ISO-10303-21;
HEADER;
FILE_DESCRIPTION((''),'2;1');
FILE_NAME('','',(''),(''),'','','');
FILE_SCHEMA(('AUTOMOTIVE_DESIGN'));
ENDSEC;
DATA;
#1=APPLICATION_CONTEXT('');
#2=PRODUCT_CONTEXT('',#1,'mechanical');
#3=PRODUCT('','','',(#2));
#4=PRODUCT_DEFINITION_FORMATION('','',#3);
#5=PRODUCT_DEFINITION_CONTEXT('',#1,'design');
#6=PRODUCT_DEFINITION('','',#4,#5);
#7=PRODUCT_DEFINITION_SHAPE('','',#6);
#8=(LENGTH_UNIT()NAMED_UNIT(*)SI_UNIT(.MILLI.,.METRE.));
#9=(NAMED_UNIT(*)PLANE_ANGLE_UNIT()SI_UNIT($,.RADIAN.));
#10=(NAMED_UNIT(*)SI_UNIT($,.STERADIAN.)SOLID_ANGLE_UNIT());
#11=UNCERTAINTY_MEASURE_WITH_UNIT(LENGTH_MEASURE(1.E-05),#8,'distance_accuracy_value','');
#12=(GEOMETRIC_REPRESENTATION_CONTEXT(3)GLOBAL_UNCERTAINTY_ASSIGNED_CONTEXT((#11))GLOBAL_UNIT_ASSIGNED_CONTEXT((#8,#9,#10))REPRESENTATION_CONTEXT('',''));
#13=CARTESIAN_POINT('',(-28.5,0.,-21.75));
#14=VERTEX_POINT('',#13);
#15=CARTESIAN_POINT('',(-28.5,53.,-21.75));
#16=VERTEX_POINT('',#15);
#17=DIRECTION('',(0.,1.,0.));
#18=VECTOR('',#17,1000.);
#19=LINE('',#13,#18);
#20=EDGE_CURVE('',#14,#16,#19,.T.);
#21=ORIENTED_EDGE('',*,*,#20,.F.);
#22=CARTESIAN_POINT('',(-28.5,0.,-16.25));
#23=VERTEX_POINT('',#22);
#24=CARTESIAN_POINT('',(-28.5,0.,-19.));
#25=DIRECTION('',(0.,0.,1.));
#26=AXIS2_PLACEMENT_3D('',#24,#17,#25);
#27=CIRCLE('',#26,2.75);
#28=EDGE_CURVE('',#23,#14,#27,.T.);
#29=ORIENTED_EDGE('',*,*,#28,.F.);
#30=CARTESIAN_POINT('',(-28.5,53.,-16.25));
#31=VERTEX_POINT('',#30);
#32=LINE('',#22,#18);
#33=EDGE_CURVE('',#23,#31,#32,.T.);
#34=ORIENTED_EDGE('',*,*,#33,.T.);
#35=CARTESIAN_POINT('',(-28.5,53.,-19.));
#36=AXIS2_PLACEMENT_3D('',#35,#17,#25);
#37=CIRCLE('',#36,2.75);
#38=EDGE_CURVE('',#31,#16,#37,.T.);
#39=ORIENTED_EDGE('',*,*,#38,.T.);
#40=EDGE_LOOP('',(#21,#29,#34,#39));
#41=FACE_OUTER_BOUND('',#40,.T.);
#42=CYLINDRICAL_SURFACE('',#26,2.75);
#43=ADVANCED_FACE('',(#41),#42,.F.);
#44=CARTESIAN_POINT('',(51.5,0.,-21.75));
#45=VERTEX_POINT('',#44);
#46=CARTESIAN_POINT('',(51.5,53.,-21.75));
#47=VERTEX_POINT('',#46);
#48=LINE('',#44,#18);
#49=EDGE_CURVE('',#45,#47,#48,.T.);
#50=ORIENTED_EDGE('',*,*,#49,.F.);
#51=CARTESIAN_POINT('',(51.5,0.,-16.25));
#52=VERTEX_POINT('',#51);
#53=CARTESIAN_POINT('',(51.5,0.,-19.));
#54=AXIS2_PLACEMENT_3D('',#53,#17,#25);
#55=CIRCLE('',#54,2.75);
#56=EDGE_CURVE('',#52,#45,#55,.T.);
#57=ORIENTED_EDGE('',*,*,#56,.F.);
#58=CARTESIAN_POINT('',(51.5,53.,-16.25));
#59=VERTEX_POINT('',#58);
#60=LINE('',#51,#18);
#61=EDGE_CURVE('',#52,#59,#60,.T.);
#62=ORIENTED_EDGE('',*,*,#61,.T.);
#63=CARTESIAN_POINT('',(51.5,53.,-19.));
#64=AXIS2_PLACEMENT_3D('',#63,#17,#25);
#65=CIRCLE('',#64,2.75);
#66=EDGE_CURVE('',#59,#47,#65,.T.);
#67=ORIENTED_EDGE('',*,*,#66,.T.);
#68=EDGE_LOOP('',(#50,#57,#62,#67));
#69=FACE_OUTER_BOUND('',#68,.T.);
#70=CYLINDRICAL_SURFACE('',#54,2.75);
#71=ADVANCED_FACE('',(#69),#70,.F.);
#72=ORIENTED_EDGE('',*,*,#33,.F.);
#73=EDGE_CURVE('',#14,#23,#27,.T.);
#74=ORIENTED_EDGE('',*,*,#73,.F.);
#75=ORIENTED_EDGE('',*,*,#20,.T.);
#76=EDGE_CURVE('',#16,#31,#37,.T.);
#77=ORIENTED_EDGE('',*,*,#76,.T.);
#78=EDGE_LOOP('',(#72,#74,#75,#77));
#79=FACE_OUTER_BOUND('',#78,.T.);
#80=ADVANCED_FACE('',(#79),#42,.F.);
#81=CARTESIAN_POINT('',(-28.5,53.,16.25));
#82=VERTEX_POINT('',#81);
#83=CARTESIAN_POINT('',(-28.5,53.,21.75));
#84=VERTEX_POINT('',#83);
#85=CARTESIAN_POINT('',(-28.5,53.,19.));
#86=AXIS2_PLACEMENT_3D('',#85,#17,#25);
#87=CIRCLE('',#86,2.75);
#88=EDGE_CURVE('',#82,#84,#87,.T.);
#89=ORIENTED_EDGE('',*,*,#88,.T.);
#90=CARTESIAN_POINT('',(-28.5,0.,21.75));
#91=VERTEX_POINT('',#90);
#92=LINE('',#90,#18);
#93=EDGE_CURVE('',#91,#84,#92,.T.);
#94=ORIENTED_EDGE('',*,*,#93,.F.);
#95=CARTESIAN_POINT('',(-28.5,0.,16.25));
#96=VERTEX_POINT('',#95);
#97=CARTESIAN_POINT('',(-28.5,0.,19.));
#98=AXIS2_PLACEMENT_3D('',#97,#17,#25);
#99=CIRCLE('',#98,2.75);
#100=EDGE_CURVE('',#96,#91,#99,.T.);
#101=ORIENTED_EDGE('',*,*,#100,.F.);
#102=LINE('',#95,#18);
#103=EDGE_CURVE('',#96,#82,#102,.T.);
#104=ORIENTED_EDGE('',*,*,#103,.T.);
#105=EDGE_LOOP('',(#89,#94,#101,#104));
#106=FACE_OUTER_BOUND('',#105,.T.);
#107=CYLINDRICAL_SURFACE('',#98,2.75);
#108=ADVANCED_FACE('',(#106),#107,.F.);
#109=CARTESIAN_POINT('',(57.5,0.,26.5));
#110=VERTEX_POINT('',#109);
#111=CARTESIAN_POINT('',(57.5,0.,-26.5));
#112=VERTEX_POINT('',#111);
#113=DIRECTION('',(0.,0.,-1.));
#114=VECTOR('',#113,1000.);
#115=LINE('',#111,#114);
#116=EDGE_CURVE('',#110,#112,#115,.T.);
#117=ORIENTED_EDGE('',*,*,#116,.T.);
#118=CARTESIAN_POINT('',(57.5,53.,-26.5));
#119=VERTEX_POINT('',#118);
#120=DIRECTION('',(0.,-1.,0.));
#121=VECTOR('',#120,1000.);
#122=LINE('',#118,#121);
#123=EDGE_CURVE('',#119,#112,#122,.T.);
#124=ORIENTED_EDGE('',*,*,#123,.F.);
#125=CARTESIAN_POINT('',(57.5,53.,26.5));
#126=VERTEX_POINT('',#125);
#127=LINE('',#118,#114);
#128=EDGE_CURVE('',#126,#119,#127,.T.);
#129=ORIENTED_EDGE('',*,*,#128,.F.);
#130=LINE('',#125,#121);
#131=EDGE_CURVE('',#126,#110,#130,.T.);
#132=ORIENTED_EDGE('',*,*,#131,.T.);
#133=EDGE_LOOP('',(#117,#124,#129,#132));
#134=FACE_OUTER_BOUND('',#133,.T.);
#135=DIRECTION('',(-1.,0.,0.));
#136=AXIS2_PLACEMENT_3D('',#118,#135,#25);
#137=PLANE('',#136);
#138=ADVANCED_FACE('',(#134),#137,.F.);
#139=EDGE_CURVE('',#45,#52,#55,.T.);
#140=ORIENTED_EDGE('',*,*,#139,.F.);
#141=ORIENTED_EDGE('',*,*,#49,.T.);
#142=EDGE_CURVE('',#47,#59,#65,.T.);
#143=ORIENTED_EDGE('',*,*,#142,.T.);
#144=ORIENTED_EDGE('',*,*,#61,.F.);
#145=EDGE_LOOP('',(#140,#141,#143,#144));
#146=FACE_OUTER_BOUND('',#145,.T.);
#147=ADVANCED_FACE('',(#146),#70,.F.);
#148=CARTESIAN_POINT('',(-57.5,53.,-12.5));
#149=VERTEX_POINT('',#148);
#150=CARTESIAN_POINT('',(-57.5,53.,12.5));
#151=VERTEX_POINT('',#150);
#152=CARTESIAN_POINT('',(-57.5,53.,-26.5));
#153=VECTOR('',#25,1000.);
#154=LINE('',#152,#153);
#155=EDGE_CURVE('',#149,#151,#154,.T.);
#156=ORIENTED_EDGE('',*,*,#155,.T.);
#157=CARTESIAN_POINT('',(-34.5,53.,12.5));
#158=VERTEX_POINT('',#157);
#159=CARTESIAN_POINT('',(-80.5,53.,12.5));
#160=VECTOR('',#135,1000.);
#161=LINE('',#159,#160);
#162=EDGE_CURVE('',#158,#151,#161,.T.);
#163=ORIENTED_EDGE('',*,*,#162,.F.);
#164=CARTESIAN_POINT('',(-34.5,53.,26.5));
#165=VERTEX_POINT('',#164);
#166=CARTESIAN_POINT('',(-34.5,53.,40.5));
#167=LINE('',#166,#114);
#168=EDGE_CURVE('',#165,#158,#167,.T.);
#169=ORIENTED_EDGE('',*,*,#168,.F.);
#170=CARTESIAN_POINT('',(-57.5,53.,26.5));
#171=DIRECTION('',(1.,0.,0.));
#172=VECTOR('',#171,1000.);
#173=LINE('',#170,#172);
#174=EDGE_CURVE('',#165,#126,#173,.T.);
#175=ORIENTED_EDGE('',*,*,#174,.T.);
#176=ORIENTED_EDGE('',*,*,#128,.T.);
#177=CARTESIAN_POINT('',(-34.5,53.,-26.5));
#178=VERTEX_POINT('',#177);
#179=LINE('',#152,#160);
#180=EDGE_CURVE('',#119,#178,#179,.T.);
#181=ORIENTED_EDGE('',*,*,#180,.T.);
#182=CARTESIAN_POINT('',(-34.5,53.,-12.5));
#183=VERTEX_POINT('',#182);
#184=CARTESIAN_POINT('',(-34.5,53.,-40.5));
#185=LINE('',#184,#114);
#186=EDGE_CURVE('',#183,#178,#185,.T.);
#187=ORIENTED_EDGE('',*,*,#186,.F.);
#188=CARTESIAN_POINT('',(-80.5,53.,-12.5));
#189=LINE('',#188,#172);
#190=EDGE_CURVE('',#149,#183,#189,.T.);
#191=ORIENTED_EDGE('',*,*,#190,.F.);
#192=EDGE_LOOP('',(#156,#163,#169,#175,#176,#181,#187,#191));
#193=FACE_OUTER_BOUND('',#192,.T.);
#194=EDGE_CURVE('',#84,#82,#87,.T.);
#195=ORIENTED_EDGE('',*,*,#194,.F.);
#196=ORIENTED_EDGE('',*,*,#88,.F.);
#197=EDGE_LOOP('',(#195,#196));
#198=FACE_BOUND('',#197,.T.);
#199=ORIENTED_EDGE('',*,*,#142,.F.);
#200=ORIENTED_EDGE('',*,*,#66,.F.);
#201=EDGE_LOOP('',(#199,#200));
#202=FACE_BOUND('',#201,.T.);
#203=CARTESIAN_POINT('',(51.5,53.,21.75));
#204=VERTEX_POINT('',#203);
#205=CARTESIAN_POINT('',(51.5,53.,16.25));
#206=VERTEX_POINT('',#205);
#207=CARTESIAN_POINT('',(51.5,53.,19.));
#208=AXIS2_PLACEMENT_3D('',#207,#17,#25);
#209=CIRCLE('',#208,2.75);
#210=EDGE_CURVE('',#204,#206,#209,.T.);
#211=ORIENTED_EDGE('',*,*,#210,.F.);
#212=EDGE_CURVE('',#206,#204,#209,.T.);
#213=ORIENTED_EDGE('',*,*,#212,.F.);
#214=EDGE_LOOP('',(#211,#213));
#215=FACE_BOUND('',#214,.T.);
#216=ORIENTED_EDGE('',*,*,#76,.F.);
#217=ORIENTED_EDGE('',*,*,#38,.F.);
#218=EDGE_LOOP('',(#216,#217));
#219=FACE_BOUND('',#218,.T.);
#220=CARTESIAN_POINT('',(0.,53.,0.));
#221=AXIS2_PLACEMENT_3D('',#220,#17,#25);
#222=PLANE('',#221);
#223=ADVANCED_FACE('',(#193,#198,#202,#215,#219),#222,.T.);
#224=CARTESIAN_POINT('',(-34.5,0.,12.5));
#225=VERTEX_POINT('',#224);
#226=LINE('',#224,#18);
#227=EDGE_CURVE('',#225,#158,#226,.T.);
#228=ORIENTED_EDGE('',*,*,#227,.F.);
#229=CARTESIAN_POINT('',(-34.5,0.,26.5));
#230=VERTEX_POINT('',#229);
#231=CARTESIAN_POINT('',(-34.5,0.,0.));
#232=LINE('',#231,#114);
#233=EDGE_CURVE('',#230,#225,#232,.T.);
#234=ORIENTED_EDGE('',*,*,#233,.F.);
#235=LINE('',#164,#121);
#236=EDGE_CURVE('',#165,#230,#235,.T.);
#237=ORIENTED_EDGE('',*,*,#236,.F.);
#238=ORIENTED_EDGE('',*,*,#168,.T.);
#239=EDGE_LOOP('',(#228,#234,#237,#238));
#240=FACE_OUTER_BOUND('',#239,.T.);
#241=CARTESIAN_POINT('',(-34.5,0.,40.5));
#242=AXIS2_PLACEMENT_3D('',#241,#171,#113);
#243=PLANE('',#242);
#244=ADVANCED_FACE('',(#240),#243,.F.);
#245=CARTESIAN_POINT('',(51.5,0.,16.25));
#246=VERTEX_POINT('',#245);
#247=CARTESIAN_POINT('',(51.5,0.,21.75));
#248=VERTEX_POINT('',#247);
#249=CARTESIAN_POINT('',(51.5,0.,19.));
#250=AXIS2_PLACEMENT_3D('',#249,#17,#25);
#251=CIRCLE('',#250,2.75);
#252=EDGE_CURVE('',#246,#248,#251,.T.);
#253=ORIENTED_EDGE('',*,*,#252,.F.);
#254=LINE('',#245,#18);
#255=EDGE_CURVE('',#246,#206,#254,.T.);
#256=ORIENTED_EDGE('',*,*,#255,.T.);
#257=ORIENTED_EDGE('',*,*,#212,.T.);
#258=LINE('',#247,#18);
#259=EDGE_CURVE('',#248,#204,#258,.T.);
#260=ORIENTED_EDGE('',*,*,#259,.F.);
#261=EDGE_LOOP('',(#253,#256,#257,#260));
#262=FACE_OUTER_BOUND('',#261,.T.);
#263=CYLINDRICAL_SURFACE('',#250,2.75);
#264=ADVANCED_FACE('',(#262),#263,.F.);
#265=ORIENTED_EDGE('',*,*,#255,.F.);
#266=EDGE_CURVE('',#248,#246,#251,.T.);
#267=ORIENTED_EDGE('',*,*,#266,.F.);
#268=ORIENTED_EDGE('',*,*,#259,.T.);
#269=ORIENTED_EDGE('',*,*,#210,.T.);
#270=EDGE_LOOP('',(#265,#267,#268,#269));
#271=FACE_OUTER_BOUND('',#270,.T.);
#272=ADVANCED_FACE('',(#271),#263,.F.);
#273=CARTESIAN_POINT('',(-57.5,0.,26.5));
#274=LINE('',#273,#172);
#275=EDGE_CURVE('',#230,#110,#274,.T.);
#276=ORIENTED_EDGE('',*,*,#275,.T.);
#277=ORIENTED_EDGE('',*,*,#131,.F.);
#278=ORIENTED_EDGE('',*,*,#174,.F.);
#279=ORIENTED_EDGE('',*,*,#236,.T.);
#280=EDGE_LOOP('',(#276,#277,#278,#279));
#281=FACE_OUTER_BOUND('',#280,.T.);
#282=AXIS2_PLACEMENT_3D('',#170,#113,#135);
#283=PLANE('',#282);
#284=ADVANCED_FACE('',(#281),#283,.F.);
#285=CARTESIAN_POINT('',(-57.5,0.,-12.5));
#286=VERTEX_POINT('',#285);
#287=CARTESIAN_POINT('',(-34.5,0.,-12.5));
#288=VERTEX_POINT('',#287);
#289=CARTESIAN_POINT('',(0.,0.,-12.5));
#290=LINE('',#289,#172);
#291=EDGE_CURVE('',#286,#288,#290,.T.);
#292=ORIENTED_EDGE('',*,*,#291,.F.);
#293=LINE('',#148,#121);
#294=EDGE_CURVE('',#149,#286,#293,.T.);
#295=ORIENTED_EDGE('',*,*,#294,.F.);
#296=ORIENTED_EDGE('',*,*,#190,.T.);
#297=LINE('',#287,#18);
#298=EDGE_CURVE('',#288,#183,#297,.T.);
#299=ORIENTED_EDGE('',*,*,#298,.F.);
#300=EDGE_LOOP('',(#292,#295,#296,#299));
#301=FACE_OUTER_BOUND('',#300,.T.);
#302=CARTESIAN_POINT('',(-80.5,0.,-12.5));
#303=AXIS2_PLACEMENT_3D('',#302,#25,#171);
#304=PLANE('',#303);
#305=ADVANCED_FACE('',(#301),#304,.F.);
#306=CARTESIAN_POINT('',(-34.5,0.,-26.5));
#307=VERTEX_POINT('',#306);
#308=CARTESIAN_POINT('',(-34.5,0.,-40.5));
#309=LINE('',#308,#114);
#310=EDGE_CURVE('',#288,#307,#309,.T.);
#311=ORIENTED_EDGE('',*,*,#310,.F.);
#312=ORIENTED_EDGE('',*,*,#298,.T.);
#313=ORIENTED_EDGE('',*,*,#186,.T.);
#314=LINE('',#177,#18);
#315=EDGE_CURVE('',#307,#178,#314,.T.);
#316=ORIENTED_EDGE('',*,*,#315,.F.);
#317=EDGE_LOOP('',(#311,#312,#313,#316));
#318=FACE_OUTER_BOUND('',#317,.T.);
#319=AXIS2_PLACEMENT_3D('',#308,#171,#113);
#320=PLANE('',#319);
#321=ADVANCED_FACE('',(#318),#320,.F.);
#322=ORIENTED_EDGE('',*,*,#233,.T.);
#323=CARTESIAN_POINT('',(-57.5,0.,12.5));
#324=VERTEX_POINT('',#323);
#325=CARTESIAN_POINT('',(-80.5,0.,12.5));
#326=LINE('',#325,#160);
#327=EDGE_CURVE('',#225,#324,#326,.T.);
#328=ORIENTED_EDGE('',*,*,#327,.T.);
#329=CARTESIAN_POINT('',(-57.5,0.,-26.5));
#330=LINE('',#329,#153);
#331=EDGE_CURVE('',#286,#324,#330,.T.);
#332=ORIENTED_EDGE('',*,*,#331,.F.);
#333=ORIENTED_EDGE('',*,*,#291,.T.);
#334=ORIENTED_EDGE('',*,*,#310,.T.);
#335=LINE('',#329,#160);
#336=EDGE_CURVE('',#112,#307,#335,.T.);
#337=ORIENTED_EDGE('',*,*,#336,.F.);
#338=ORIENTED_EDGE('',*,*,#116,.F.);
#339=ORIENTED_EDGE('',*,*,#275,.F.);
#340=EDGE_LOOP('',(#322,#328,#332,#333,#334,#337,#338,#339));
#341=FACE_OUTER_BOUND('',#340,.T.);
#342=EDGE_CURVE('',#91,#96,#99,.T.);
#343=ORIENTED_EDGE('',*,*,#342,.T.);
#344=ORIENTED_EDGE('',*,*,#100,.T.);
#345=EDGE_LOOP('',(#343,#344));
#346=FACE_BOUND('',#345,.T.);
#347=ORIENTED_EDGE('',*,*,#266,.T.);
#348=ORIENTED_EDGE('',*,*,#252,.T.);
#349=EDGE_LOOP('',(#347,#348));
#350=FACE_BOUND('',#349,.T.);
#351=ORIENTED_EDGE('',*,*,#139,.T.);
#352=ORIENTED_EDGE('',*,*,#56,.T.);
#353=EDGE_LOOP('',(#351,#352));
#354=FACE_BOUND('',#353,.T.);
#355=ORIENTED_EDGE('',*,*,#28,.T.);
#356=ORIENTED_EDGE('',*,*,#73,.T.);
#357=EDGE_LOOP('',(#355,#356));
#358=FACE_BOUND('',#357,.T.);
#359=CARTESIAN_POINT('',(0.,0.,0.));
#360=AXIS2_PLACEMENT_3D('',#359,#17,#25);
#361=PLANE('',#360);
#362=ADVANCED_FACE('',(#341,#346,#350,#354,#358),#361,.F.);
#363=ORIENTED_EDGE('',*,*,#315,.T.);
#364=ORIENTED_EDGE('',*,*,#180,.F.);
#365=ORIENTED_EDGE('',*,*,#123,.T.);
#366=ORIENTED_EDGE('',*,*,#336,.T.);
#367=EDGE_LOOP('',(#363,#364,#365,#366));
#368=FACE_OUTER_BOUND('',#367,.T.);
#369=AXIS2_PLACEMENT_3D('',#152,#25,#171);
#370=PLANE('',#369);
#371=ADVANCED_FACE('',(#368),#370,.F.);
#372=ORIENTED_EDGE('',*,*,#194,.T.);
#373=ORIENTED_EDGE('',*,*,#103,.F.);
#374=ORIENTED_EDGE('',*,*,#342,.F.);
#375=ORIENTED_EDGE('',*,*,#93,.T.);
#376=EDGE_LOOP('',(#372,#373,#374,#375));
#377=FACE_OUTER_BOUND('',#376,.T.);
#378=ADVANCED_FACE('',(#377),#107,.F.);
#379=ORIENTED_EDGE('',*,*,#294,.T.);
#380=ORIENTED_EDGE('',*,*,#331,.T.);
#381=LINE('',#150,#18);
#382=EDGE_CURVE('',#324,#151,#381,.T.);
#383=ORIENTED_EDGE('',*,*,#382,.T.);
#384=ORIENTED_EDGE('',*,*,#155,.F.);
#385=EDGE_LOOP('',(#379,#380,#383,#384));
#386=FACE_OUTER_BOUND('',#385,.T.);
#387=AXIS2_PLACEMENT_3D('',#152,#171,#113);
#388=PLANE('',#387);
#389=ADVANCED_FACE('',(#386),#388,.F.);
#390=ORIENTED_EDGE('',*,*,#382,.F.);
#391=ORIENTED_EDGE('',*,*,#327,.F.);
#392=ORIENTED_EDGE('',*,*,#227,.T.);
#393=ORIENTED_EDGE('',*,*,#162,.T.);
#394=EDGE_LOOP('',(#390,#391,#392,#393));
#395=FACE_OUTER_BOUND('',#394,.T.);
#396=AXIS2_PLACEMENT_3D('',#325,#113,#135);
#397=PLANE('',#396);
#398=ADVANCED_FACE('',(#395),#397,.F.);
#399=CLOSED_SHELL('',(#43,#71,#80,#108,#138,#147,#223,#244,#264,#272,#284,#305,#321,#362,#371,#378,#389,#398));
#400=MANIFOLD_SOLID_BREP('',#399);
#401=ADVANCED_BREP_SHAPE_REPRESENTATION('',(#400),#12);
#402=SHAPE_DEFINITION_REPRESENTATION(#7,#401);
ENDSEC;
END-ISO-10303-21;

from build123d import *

# Parameters (mm, degrees)
SKETCH_1_W          = 115
SKETCH_1_H          = 53
EXTRUDE_1_DEPTH     = 53
SKETCH_2_W          = 46
SKETCH_2_H          = 28
CUT_EXTRUDE_1_DEPTH = 83.568153667
SKETCH_3_R          = 2.75
CUT_EXTRUDE_2_DEPTH = 83.568153667


with BuildPart() as part:
    # 草图1 → 凸台-拉伸1 (new body)
    with BuildSketch(Plane(origin=(0, 0, 0), x_dir=(1, 0, 0), z_dir=(0, 1, 0))):
        Rectangle(SKETCH_1_W, SKETCH_1_H)
    extrude(amount=EXTRUDE_1_DEPTH)

    # 草图2 → 切除-拉伸1 (cut, through all)
    with BuildSketch(Plane(origin=(0, 53, 0), x_dir=(1, 0, 0), z_dir=(0, 1, 0))):
        with Locations((-57.5, -26.5)):
            Rectangle(SKETCH_2_W, SKETCH_2_H)
        with Locations((-57.5, 26.5)):
            Rectangle(SKETCH_2_W, SKETCH_2_H)
    extrude(amount=-CUT_EXTRUDE_1_DEPTH, mode=Mode.SUBTRACT)

    # 草图3 → 切除-拉伸2 (cut, through all)
    with BuildSketch(Plane(origin=(0, 53, 0), x_dir=(1, 0, 0), z_dir=(0, 1, 0))):
        with Locations(Location((-28.5, 19, 0), (0, 0, 270))):
            Circle(SKETCH_3_R)
        with Locations(Location((51.5, 19, 0), (0, 0, 270))):
            Circle(SKETCH_3_R)
        with Locations(Location((51.5, -19, 0), (0, 0, 270))):
            Circle(SKETCH_3_R)
        with Locations(Location((-28.5, -19, 0), (0, 0, 270))):
            Circle(SKETCH_3_R)
    extrude(amount=-CUT_EXTRUDE_2_DEPTH, mode=Mode.SUBTRACT)


solid = part.part
